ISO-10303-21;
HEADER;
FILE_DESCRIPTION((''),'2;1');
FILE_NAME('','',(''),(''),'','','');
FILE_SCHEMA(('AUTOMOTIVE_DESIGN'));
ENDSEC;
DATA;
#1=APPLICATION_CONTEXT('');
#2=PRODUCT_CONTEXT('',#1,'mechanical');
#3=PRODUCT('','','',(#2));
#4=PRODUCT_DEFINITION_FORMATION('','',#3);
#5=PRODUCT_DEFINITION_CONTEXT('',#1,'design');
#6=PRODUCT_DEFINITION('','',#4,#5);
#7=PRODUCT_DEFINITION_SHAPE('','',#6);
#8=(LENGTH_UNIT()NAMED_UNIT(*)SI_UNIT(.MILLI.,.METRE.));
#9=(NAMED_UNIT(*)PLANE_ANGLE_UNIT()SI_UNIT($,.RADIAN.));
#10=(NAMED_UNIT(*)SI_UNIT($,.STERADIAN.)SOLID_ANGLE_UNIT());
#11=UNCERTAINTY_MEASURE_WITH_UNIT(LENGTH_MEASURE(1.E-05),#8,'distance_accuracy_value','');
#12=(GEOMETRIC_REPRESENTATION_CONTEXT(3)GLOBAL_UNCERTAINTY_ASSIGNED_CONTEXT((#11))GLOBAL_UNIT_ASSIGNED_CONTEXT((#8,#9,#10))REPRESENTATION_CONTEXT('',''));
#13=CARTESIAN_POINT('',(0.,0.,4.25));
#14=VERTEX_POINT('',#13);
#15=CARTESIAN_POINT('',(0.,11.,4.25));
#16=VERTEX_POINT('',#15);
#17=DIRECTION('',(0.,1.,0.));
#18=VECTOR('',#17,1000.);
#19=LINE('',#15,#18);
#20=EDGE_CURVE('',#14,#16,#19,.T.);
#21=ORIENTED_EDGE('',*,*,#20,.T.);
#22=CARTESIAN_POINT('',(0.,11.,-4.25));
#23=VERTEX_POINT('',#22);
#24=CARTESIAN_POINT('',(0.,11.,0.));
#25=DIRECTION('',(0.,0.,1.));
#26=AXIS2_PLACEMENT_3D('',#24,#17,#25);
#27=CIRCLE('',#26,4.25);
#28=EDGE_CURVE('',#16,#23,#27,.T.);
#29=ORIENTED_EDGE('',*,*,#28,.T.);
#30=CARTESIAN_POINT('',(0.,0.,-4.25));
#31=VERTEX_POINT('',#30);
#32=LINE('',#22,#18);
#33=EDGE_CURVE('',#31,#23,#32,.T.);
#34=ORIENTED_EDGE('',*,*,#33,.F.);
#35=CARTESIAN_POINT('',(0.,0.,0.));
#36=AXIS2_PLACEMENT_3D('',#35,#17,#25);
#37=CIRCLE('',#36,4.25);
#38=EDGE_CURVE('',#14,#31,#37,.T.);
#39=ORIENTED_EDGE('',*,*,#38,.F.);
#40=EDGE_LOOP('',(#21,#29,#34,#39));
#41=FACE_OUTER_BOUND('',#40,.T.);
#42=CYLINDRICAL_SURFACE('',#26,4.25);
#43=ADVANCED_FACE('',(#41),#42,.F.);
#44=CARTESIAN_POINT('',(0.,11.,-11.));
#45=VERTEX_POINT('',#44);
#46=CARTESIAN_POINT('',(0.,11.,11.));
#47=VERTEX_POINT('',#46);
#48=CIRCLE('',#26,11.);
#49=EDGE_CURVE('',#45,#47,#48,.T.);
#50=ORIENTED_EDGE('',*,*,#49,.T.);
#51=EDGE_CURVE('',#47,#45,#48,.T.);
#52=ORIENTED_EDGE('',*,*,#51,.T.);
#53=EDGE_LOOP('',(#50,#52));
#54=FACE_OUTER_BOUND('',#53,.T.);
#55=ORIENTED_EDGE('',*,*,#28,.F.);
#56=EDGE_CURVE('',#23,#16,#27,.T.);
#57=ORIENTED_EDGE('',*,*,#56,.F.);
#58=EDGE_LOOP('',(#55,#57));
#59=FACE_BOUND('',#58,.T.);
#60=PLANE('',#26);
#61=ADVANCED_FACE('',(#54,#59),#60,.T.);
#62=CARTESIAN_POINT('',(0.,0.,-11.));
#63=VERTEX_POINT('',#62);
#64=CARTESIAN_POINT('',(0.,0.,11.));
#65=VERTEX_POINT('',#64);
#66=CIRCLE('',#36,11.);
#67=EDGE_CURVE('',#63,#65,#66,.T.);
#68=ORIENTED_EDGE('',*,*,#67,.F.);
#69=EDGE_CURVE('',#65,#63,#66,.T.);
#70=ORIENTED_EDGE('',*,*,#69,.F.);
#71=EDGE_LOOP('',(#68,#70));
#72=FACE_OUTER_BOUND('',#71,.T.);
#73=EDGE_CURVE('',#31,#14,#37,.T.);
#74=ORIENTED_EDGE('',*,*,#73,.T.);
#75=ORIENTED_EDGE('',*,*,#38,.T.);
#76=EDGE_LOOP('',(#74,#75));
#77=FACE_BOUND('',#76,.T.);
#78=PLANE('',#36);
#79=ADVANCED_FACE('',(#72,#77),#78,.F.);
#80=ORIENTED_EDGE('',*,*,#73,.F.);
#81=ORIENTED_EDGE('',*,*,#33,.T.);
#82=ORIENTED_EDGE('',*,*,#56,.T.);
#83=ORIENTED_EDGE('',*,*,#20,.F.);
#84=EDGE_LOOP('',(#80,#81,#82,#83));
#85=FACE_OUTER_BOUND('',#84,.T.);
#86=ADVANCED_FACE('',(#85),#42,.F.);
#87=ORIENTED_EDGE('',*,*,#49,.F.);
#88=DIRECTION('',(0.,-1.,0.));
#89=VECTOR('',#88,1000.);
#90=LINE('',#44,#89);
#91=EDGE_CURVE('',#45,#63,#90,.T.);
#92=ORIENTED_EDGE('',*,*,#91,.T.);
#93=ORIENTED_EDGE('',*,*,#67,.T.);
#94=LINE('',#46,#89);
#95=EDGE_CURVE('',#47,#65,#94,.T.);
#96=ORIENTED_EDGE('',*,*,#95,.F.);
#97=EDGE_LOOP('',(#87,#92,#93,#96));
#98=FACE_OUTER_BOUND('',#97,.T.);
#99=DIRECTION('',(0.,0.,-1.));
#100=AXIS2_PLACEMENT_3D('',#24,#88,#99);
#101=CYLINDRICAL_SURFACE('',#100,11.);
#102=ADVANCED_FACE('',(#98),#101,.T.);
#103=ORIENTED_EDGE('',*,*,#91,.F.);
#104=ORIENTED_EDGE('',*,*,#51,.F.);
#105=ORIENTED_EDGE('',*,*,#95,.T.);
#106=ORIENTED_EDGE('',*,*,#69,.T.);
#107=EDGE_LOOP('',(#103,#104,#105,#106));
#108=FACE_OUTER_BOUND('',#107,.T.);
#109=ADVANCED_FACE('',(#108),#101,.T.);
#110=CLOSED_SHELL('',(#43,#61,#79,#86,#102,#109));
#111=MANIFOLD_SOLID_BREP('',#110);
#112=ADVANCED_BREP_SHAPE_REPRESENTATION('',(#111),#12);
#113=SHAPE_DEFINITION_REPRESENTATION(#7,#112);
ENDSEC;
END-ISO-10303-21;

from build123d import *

# Parameters (mm, degrees)
SKETCH1_R              = 11
SKETCH1_R_2            = 4
BOSS_EXTRUDE1_DEPTH    = 11
M10_TAPPED_HOLE1_D     = 8.5
M10_TAPPED_HOLE1_DEPTH = 24.5
M10_TAPPED_HOLE1_TIP   = 2.553657631


with BuildPart() as part:
    # Sketch1 → Boss-Extrude1 (new body)
    with BuildSketch(Plane(origin=(0, 0, 0), x_dir=(1, 0, 0), z_dir=(0, 1, 0))):
        with Locations(Location((0, 0, 0), (0, 0, 270))):
            Circle(SKETCH1_R)
        with Locations(Location((0, 0, 0), (0, 0, 270))):
            Circle(SKETCH1_R_2, mode=Mode.SUBTRACT)
    extrude(amount=BOSS_EXTRUDE1_DEPTH)

    # M10 Tapped Hole1
    with Locations(Plane(origin=(0, 11, 0), x_dir=(1, 0, 0), z_dir=(0, 1, 0))):
        with Locations((0, 0)):
            Hole(M10_TAPPED_HOLE1_D / 2, depth=M10_TAPPED_HOLE1_DEPTH)
            with Locations((0, 0, -(M10_TAPPED_HOLE1_DEPTH + M10_TAPPED_HOLE1_TIP / 2))):  # 118° drill point
                Cone(0, M10_TAPPED_HOLE1_D / 2, M10_TAPPED_HOLE1_TIP, mode=Mode.SUBTRACT)


solid = part.part
